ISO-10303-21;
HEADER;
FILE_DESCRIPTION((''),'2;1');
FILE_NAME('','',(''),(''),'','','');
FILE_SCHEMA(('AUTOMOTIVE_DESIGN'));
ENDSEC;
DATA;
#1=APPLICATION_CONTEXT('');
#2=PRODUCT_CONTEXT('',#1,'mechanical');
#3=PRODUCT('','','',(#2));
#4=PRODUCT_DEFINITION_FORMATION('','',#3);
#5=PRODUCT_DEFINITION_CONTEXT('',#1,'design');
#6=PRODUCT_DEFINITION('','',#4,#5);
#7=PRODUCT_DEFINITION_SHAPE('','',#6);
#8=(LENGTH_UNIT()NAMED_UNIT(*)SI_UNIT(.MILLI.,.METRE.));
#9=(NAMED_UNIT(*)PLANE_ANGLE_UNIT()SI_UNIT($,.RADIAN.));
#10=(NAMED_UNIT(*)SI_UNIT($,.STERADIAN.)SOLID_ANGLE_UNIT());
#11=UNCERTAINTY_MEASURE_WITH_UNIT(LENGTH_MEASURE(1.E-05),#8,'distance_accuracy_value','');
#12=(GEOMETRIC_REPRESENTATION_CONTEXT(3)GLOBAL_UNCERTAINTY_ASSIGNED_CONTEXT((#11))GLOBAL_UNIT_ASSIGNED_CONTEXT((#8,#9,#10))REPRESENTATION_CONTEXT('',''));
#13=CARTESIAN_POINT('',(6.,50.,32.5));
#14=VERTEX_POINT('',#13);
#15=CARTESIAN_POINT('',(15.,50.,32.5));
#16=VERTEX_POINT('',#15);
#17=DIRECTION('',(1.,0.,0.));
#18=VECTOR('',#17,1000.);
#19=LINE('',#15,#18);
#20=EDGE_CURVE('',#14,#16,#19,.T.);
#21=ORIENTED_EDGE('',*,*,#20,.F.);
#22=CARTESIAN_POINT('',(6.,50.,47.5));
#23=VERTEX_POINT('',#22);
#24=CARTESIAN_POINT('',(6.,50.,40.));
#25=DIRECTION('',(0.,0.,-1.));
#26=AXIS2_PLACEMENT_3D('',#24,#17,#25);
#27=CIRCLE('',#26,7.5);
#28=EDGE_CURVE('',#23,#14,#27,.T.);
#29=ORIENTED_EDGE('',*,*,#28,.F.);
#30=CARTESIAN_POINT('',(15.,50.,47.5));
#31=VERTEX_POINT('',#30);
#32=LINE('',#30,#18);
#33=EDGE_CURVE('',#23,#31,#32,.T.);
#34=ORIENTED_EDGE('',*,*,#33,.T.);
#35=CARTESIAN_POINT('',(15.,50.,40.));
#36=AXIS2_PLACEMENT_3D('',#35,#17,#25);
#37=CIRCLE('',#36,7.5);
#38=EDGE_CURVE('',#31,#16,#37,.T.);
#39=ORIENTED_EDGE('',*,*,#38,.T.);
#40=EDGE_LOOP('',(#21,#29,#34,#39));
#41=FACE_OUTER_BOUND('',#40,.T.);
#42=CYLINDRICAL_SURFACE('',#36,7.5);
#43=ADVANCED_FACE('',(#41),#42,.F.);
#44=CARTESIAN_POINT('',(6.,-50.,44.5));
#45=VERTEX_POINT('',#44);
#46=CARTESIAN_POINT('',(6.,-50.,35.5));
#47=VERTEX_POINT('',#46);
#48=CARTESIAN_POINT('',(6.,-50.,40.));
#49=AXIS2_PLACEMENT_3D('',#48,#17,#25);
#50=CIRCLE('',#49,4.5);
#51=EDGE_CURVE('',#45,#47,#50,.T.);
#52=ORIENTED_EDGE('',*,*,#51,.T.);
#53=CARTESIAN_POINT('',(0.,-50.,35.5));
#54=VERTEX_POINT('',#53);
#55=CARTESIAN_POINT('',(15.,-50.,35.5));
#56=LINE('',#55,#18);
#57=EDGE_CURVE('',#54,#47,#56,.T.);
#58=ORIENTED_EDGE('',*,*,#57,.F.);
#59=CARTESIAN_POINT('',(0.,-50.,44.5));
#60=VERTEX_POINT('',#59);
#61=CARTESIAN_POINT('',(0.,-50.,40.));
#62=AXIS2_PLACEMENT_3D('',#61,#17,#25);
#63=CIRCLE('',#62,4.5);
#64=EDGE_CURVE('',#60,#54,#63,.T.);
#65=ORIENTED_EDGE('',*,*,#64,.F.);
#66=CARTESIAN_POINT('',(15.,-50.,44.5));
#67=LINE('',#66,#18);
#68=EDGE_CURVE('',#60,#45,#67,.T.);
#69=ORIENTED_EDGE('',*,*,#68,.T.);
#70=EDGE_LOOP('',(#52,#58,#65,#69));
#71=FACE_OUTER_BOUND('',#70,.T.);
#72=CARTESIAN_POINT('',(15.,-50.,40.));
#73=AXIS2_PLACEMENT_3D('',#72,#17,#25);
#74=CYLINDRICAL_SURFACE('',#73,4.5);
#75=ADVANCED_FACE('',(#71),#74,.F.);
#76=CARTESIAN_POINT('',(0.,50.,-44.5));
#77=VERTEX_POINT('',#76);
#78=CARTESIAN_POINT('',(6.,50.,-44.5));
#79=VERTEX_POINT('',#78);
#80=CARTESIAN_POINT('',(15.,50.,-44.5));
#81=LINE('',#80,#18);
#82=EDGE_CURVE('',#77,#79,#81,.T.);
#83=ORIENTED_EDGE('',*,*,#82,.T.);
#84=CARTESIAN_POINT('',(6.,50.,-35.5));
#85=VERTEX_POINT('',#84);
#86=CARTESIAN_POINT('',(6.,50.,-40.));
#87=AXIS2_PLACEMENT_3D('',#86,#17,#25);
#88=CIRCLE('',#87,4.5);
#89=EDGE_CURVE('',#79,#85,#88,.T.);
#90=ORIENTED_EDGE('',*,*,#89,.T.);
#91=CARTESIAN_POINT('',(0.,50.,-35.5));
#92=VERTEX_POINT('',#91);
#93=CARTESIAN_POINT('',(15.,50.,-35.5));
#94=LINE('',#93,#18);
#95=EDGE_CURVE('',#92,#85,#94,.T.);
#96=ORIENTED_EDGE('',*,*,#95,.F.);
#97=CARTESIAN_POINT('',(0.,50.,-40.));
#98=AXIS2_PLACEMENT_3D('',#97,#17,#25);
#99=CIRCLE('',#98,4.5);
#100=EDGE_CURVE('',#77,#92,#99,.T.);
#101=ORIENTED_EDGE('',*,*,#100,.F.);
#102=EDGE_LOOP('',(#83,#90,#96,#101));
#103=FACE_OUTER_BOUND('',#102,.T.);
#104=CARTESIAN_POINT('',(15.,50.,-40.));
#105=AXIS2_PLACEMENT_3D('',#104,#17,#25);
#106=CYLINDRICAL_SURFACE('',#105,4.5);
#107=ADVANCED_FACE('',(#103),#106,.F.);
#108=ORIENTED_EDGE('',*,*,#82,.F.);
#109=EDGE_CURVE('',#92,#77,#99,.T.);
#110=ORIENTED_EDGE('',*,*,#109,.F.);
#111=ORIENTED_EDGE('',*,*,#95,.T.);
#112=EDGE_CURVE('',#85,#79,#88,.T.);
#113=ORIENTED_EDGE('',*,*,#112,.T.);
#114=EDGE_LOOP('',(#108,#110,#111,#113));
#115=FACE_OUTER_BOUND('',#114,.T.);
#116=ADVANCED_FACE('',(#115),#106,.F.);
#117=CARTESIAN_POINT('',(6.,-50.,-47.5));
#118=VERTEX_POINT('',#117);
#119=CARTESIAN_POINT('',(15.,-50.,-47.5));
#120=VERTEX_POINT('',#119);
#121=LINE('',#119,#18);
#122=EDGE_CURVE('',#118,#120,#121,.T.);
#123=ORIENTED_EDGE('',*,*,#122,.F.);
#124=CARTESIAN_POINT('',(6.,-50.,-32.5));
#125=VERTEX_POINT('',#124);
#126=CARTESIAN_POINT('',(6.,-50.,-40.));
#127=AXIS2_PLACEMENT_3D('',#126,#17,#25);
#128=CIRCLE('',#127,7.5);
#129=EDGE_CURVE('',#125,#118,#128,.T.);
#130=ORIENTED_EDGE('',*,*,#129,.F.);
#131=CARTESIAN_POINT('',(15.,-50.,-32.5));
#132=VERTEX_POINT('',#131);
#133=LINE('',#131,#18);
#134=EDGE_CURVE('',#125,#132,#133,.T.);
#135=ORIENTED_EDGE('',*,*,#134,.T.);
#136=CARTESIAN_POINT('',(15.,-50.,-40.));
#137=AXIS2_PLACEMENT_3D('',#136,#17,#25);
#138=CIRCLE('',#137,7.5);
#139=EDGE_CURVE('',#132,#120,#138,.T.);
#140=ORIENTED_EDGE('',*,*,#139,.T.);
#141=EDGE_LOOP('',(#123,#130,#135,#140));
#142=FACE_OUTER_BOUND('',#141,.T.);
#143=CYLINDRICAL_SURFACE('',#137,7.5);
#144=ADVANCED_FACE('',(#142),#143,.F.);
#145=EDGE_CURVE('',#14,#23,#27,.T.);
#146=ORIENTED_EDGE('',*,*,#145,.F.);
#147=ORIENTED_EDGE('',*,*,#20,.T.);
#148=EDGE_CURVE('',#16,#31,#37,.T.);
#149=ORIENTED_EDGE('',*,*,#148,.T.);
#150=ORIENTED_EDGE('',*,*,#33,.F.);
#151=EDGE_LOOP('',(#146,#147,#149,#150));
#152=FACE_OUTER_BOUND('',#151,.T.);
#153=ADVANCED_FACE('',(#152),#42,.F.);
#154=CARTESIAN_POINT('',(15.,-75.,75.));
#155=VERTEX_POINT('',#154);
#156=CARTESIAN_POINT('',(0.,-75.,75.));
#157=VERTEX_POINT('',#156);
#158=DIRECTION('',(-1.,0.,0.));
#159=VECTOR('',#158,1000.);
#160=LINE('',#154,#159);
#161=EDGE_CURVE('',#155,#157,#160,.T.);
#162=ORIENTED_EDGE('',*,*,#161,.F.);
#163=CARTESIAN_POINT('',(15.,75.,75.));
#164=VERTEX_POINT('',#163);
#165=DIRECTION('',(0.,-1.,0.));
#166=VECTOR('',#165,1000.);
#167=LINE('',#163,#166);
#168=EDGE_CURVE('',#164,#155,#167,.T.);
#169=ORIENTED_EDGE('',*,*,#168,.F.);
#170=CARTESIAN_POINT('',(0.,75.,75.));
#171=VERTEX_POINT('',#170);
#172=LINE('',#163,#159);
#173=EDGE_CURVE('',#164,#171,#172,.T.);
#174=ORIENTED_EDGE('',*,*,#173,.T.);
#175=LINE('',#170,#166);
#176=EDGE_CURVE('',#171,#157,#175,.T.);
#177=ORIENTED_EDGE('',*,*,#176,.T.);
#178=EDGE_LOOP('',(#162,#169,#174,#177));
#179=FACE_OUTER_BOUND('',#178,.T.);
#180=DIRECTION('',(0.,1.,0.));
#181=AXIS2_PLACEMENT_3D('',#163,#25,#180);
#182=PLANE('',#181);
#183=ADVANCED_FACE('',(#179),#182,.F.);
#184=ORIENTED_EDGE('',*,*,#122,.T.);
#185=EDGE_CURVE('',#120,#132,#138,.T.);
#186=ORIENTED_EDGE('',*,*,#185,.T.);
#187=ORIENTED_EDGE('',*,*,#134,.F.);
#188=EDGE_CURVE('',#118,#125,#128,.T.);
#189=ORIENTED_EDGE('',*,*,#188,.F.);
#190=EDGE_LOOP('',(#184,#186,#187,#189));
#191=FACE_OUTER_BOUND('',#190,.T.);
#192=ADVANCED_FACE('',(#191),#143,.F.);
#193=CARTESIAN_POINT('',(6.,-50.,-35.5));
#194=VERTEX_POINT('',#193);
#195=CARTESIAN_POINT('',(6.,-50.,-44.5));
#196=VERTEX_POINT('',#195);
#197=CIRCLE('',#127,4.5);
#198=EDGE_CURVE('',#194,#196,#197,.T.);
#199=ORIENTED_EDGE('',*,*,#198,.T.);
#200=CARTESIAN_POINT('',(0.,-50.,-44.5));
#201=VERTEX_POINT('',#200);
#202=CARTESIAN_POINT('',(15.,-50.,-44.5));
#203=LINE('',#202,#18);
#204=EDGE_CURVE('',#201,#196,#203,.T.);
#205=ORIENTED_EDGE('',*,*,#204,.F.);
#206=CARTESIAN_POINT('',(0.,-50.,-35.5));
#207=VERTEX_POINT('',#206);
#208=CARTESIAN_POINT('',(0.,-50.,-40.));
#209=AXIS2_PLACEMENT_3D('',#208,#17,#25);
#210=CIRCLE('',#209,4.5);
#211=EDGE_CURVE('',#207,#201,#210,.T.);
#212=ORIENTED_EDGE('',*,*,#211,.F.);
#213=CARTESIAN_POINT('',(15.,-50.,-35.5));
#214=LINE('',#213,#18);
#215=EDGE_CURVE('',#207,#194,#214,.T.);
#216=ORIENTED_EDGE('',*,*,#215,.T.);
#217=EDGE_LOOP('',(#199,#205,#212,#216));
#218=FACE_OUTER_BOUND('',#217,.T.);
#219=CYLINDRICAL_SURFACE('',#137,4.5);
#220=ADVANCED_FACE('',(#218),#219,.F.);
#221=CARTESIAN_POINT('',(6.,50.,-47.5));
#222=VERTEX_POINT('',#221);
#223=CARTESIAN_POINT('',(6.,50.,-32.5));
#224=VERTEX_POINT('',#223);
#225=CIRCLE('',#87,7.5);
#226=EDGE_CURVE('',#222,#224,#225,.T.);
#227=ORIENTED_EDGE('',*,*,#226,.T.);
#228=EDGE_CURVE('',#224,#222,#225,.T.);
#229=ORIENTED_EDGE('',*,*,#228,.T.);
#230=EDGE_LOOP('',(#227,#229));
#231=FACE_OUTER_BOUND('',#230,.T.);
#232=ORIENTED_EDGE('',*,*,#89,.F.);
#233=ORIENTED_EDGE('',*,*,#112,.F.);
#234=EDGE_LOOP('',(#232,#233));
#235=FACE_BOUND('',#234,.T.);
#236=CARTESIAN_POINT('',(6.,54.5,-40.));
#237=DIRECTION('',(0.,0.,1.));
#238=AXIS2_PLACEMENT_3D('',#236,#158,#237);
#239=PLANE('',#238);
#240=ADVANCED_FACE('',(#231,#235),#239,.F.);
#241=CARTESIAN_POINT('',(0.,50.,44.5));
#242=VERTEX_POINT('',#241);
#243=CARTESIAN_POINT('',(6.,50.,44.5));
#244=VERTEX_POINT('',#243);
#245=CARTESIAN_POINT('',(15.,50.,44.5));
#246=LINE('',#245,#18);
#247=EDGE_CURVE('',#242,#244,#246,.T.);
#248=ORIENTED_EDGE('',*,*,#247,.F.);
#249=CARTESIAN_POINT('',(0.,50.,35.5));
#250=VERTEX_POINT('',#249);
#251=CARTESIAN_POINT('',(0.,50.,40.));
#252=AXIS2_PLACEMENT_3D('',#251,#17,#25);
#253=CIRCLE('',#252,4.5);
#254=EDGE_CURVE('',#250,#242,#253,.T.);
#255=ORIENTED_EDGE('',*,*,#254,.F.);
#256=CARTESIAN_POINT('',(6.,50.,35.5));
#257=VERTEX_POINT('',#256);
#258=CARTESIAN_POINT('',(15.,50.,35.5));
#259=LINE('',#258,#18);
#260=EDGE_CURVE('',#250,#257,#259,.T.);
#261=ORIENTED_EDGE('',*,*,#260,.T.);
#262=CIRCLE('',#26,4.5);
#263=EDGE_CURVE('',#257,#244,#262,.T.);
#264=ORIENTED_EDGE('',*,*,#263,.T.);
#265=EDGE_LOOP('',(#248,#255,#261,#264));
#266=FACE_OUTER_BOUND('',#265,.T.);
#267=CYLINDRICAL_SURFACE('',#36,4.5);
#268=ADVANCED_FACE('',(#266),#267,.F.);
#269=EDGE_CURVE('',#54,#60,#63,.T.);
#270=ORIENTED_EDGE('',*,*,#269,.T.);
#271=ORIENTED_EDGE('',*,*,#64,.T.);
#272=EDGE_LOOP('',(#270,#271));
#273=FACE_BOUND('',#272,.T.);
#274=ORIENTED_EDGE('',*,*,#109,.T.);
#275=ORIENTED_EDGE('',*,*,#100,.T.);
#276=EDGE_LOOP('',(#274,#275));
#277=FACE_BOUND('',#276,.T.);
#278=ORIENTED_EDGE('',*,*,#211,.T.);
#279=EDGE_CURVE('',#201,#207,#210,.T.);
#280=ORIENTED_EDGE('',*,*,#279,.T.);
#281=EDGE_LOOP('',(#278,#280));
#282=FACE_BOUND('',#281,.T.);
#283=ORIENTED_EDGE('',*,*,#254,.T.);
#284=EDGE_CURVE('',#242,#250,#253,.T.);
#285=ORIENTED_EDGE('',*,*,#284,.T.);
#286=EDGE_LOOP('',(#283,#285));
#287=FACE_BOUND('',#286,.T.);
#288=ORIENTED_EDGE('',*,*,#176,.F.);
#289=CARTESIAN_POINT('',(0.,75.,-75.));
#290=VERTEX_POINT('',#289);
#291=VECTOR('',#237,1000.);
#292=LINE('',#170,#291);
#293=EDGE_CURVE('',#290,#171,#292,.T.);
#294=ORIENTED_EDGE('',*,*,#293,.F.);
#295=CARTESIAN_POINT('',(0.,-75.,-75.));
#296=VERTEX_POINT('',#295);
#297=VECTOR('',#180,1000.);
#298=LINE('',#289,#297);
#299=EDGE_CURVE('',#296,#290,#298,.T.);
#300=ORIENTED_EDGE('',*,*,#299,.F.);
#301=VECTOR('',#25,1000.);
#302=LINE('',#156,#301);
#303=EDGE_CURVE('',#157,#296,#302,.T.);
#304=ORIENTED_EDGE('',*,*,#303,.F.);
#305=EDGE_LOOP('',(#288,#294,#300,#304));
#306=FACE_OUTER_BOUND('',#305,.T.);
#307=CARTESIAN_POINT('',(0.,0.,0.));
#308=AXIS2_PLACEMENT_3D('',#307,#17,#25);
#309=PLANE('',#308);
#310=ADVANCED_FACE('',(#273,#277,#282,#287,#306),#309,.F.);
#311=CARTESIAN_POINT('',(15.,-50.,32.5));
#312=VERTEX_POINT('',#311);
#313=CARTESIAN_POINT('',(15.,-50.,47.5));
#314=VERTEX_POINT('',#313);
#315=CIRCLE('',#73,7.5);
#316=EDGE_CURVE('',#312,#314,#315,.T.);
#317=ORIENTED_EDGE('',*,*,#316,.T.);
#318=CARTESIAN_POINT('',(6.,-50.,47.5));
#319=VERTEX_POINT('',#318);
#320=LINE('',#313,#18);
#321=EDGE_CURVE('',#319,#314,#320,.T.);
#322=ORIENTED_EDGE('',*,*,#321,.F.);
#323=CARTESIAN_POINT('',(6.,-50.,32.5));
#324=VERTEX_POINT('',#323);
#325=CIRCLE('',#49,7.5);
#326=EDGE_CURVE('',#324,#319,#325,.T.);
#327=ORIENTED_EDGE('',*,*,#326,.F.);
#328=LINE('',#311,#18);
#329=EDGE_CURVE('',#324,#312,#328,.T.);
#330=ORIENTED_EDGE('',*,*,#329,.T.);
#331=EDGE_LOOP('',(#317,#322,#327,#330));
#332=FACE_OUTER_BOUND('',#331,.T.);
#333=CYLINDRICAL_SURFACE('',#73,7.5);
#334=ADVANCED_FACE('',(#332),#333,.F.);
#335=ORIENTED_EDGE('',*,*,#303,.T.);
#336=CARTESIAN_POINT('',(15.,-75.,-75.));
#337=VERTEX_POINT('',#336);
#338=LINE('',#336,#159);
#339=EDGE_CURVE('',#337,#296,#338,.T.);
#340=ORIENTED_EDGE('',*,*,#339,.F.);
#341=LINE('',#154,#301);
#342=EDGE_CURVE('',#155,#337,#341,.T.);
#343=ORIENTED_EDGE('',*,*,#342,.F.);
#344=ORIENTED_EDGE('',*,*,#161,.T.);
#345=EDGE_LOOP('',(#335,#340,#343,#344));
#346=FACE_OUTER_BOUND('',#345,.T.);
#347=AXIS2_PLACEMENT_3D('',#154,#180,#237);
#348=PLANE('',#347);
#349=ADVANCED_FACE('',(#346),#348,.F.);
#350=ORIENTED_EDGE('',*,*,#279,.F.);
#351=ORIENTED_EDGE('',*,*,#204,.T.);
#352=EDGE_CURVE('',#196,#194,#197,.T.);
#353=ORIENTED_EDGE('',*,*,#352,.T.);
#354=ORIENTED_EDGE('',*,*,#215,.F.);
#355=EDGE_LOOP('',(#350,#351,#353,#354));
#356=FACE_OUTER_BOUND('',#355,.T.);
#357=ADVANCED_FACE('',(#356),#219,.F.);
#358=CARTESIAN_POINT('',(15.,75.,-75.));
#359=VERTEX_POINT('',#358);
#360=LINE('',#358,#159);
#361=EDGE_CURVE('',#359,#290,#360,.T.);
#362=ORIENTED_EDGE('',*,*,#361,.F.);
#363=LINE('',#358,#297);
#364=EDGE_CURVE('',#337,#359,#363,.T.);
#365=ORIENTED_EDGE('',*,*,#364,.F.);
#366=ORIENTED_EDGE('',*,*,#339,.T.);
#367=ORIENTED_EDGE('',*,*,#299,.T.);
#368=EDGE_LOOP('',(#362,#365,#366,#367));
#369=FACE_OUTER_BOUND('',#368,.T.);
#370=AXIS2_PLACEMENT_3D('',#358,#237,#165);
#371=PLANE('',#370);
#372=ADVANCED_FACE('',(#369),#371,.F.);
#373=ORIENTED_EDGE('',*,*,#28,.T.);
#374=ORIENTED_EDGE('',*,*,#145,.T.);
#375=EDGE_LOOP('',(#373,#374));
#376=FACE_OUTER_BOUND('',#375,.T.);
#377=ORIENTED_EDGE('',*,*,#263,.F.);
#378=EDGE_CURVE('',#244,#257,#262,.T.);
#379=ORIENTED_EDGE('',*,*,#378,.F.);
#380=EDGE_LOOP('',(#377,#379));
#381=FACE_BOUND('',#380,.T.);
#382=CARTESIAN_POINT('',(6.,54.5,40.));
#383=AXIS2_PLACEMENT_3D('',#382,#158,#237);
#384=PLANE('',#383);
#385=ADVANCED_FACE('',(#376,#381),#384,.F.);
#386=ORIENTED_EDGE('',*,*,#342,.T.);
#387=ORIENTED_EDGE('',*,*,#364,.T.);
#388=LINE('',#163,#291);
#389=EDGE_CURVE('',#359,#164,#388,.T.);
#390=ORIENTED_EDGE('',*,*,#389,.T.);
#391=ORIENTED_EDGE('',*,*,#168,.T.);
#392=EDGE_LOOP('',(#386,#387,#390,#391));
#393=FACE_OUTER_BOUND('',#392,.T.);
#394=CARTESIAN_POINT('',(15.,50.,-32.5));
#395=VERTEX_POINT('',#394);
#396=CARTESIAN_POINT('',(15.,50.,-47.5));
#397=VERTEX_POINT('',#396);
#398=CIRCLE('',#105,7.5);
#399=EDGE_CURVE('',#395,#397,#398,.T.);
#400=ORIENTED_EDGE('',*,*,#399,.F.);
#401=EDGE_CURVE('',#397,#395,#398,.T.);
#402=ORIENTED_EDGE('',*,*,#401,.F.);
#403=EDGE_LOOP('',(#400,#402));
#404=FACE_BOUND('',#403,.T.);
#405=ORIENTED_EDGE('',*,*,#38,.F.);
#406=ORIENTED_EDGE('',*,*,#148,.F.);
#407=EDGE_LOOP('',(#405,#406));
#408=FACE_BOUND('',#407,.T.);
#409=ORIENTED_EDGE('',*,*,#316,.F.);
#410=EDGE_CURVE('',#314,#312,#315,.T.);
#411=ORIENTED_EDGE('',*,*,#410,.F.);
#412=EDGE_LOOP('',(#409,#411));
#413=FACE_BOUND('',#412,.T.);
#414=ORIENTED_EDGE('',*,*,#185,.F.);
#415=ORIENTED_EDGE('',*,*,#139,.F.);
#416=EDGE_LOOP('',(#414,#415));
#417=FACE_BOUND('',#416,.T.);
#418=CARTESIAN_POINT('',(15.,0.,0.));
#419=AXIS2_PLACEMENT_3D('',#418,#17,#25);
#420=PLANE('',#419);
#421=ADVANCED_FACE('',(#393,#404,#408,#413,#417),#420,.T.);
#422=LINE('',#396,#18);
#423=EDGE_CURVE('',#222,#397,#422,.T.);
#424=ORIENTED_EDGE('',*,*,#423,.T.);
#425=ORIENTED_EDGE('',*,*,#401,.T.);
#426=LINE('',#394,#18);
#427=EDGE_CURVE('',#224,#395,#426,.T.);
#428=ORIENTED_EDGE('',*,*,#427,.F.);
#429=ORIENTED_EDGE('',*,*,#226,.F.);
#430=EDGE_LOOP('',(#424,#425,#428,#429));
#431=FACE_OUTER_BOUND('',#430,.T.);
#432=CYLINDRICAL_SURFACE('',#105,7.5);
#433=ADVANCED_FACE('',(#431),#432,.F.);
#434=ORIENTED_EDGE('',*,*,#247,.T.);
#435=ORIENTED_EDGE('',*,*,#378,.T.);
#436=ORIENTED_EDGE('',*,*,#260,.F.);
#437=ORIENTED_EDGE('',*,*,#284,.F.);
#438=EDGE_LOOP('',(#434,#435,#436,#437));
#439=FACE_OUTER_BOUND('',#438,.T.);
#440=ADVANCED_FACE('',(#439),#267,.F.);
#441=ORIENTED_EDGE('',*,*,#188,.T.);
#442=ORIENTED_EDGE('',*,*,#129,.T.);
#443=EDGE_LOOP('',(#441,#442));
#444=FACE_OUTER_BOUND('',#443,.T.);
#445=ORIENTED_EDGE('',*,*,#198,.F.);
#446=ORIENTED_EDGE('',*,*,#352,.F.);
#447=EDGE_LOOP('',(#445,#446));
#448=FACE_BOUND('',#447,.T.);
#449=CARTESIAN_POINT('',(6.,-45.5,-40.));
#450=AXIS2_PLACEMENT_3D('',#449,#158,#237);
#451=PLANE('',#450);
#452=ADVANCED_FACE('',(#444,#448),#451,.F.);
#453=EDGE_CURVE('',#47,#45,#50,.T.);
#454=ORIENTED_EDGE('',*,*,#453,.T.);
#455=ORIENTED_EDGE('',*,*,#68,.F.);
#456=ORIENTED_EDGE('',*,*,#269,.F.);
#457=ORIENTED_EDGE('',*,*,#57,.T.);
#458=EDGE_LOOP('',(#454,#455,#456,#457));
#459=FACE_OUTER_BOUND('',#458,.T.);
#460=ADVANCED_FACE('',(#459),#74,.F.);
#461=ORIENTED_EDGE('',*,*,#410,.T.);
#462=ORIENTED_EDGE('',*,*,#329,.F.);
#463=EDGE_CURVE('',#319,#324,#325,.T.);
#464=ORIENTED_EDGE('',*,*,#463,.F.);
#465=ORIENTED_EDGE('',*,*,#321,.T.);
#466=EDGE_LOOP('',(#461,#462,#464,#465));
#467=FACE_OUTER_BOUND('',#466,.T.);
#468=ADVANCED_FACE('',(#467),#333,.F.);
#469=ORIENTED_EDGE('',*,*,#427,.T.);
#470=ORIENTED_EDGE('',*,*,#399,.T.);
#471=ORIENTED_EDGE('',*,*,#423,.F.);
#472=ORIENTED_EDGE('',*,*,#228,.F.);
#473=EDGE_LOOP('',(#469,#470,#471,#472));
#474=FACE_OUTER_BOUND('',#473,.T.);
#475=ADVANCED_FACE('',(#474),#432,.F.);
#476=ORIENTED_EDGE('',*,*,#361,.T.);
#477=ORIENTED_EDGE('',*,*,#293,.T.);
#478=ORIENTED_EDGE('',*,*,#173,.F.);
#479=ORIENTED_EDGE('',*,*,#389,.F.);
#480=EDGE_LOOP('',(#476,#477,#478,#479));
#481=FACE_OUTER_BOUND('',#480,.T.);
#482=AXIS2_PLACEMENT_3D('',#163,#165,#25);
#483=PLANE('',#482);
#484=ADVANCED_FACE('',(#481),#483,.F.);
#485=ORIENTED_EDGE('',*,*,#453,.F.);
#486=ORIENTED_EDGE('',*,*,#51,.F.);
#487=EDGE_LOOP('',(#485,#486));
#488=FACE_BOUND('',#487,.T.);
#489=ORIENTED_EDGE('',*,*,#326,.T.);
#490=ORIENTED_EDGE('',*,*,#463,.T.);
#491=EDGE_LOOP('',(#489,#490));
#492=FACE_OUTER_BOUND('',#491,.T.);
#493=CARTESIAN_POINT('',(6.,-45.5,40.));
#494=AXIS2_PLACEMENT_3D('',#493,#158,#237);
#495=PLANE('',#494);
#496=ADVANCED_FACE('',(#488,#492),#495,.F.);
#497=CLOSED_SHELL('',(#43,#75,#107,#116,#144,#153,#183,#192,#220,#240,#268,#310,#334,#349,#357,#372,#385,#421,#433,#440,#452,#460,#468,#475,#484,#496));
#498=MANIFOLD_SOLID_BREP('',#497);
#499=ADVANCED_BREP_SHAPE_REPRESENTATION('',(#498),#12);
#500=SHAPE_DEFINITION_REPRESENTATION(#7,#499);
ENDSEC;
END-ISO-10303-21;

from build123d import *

# Parameters (mm, degrees)
SKETCH_1_W                = 150
SKETCH_1_H                = 150
EXTRUDE_1_DEPTH           = 15
HOLE_WIZARD_1_D           = 9
HOLE_WIZARD_1_CBORE_D     = 15
HOLE_WIZARD_1_CBORE_DEPTH = 9


with BuildPart() as part:
    # 草图1 → 凸台-拉伸1 (new body)
    with BuildSketch(Plane(origin=(0, 0, 0), x_dir=(0, 0, -1), z_dir=(1, 0, 0))):
        Rectangle(SKETCH_1_W, SKETCH_1_H)
    extrude(amount=EXTRUDE_1_DEPTH)

    # 打孔尺寸(%根据)内六角圆柱头螺钉的类型1 (through all)
    with Locations(Plane(origin=(15, 0, 0), x_dir=(0, 0, -1), z_dir=(1, 0, 0))):
        with Locations((-40, 50), (40, 50), (-40, -50), (40, -50)):
            CounterBoreHole(HOLE_WIZARD_1_D / 2, HOLE_WIZARD_1_CBORE_D / 2, HOLE_WIZARD_1_CBORE_DEPTH)


solid = part.part
